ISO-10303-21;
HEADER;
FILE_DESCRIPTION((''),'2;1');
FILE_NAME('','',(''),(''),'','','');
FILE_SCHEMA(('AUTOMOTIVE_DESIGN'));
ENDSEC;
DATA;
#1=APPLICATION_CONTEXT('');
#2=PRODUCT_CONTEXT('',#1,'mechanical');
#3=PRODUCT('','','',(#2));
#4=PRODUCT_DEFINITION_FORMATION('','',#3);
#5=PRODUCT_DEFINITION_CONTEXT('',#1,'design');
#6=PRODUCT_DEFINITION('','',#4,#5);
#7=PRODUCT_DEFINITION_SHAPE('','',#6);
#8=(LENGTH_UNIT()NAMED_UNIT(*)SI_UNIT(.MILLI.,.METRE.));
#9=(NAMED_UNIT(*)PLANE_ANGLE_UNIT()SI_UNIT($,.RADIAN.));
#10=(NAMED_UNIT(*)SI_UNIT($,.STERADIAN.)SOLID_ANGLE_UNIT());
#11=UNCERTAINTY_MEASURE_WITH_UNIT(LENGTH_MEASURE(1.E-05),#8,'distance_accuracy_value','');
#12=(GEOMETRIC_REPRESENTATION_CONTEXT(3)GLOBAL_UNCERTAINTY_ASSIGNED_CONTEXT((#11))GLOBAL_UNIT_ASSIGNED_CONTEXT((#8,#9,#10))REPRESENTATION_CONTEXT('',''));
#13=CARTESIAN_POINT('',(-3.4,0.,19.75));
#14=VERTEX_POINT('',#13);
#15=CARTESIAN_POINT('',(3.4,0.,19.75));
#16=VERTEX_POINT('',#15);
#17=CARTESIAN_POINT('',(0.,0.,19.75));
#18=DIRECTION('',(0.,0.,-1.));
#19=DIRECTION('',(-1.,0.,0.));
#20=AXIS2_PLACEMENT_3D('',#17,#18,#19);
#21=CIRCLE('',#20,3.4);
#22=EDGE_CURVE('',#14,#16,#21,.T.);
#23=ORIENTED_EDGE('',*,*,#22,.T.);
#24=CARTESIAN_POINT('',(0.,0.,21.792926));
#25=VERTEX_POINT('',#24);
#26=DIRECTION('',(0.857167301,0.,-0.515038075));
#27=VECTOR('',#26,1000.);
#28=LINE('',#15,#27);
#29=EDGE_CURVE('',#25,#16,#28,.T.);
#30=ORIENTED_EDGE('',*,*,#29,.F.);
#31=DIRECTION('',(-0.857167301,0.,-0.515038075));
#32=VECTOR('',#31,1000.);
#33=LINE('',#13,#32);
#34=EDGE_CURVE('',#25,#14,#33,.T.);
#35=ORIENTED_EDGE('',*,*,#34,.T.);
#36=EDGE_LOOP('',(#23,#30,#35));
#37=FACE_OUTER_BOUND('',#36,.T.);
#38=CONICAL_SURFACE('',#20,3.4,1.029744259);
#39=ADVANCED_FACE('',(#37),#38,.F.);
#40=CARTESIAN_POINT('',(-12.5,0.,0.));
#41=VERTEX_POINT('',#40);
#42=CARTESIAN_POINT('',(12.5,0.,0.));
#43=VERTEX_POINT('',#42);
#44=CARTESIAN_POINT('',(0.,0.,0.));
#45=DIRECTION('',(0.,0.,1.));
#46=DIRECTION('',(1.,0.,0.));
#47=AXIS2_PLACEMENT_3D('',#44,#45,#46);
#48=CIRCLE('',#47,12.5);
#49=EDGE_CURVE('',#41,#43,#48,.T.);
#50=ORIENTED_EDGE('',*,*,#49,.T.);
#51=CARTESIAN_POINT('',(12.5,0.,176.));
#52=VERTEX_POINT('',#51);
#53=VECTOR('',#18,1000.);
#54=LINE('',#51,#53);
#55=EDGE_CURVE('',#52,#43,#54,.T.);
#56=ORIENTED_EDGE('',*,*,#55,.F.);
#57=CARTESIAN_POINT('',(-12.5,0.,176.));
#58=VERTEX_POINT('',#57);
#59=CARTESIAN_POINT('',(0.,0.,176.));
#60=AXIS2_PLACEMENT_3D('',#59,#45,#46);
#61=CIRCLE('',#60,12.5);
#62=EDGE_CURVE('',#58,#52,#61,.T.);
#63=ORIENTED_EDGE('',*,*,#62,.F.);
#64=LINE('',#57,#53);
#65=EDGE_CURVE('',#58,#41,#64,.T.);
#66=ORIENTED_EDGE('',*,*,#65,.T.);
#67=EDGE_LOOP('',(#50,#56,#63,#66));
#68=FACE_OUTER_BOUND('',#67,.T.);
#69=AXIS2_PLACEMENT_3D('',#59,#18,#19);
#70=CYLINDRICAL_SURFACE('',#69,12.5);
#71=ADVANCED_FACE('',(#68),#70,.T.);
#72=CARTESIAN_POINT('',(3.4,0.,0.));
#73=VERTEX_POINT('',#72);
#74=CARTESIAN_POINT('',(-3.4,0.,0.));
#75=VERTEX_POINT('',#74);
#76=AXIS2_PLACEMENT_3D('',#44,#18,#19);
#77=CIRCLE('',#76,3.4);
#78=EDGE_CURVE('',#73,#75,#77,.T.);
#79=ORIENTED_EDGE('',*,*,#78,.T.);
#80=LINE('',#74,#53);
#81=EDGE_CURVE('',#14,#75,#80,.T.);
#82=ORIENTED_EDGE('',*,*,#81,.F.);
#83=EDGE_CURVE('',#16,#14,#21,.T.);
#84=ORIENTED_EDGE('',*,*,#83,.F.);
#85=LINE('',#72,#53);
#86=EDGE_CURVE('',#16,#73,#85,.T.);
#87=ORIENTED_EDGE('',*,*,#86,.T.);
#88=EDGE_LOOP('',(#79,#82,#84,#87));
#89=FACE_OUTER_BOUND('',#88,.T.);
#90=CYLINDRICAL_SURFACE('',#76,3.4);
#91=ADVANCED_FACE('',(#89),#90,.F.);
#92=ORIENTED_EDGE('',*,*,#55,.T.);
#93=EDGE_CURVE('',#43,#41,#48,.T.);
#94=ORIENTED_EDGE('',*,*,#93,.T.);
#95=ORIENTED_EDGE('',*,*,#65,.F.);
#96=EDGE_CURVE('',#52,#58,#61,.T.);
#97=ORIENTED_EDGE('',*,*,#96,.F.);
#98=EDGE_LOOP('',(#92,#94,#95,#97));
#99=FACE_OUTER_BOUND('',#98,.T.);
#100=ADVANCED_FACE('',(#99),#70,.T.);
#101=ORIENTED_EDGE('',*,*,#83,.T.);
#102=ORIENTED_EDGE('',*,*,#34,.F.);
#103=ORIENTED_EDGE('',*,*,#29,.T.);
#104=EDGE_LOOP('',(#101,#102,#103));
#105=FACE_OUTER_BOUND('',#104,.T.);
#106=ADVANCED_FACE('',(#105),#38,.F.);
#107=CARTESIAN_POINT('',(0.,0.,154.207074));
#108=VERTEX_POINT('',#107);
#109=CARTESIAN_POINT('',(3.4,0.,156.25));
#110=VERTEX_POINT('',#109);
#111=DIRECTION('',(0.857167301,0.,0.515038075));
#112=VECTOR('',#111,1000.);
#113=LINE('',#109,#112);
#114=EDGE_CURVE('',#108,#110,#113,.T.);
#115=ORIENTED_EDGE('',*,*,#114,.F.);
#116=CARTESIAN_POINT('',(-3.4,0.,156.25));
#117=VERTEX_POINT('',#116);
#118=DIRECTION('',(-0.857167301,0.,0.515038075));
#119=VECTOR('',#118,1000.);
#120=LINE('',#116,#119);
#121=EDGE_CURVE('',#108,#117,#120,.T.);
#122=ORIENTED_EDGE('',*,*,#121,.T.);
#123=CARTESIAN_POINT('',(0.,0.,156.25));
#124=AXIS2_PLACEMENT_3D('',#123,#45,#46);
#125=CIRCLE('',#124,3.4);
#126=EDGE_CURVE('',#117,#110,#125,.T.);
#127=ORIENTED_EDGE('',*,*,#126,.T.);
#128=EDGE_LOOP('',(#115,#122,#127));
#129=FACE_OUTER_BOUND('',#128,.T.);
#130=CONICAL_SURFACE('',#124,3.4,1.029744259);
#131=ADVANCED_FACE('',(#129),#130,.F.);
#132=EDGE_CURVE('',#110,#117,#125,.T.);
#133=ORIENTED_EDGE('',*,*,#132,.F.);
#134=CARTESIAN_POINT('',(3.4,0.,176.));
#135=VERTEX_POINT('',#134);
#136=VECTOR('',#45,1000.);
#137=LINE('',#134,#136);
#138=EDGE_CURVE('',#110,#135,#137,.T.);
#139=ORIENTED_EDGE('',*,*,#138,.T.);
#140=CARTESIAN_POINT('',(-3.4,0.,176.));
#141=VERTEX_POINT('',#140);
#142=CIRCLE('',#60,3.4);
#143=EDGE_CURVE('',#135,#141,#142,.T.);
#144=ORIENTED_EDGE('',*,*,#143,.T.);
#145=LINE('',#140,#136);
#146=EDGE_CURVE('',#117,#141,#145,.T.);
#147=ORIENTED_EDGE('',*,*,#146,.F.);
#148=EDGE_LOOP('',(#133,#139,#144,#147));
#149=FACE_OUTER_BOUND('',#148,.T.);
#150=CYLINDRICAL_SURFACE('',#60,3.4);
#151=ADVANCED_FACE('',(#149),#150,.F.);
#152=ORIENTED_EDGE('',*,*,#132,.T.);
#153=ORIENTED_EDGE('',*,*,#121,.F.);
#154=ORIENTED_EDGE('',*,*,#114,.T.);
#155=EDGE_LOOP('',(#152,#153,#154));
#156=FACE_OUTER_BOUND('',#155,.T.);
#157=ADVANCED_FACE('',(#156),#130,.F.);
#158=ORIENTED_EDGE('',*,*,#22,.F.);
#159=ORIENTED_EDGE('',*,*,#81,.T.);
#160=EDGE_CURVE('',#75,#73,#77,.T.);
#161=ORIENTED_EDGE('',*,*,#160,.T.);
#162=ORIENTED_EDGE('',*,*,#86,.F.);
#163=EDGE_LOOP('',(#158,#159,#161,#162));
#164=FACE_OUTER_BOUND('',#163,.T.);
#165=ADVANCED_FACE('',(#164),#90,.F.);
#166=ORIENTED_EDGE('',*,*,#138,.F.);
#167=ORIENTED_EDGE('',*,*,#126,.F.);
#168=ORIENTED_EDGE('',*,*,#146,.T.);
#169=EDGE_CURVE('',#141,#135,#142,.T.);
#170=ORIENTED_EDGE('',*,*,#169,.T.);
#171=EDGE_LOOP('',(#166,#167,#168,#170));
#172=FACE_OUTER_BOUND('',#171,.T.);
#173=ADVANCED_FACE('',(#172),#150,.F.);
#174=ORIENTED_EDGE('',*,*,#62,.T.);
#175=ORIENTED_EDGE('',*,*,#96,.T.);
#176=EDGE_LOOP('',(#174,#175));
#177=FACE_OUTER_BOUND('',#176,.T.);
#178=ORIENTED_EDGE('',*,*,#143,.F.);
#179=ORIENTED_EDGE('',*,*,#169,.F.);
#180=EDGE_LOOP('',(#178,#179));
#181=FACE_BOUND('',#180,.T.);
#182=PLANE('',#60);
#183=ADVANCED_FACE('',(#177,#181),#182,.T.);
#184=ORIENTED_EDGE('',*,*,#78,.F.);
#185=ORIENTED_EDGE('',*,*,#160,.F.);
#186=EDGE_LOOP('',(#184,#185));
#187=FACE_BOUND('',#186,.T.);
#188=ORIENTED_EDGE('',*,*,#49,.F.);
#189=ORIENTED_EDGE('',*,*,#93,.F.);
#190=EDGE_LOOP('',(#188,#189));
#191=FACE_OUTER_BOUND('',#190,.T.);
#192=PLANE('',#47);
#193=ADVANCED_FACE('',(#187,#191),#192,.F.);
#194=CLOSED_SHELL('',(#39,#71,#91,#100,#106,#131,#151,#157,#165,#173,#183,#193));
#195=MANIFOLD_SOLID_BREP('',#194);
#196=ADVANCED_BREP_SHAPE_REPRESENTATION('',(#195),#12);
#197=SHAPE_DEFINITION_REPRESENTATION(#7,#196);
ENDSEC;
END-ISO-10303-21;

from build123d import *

# Parameters (mm, degrees)
SKETCH_1_R             = 12.5
EXTRUDE_1_DEPTH        = 176
HOLE_WIZARD_M8_1_D     = 6.8
HOLE_WIZARD_M8_1_DEPTH = 19.75
HOLE_WIZARD_M8_1_TIP   = 2.042926105
HOLE_WIZARD_M8_2_D     = 6.8
HOLE_WIZARD_M8_2_DEPTH = 19.75
HOLE_WIZARD_M8_2_TIP   = 2.042926105


with BuildPart() as part:
    # 草图1 → 凸台-拉伸1 (new body)
    with BuildSketch(Plane.XY):
        Circle(SKETCH_1_R)
    extrude(amount=EXTRUDE_1_DEPTH)

    # M8 螺纹孔1
    with Locations(Plane(origin=(0, 0, 0), x_dir=(-1, 0, 0), z_dir=(0, 0, -1))):
        with Locations((0, 0)):
            Hole(HOLE_WIZARD_M8_1_D / 2, depth=HOLE_WIZARD_M8_1_DEPTH)
            with Locations((0, 0, -(HOLE_WIZARD_M8_1_DEPTH + HOLE_WIZARD_M8_1_TIP / 2))):  # 118° drill point
                Cone(0, HOLE_WIZARD_M8_1_D / 2, HOLE_WIZARD_M8_1_TIP, mode=Mode.SUBTRACT)

    # M8 螺纹孔2
    with Locations(Plane.XY.offset(176)):
        with Locations((0, 0)):
            Hole(HOLE_WIZARD_M8_2_D / 2, depth=HOLE_WIZARD_M8_2_DEPTH)
            with Locations((0, 0, -(HOLE_WIZARD_M8_2_DEPTH + HOLE_WIZARD_M8_2_TIP / 2))):  # 118° drill point
                Cone(0, HOLE_WIZARD_M8_2_D / 2, HOLE_WIZARD_M8_2_TIP, mode=Mode.SUBTRACT)


solid = part.part
